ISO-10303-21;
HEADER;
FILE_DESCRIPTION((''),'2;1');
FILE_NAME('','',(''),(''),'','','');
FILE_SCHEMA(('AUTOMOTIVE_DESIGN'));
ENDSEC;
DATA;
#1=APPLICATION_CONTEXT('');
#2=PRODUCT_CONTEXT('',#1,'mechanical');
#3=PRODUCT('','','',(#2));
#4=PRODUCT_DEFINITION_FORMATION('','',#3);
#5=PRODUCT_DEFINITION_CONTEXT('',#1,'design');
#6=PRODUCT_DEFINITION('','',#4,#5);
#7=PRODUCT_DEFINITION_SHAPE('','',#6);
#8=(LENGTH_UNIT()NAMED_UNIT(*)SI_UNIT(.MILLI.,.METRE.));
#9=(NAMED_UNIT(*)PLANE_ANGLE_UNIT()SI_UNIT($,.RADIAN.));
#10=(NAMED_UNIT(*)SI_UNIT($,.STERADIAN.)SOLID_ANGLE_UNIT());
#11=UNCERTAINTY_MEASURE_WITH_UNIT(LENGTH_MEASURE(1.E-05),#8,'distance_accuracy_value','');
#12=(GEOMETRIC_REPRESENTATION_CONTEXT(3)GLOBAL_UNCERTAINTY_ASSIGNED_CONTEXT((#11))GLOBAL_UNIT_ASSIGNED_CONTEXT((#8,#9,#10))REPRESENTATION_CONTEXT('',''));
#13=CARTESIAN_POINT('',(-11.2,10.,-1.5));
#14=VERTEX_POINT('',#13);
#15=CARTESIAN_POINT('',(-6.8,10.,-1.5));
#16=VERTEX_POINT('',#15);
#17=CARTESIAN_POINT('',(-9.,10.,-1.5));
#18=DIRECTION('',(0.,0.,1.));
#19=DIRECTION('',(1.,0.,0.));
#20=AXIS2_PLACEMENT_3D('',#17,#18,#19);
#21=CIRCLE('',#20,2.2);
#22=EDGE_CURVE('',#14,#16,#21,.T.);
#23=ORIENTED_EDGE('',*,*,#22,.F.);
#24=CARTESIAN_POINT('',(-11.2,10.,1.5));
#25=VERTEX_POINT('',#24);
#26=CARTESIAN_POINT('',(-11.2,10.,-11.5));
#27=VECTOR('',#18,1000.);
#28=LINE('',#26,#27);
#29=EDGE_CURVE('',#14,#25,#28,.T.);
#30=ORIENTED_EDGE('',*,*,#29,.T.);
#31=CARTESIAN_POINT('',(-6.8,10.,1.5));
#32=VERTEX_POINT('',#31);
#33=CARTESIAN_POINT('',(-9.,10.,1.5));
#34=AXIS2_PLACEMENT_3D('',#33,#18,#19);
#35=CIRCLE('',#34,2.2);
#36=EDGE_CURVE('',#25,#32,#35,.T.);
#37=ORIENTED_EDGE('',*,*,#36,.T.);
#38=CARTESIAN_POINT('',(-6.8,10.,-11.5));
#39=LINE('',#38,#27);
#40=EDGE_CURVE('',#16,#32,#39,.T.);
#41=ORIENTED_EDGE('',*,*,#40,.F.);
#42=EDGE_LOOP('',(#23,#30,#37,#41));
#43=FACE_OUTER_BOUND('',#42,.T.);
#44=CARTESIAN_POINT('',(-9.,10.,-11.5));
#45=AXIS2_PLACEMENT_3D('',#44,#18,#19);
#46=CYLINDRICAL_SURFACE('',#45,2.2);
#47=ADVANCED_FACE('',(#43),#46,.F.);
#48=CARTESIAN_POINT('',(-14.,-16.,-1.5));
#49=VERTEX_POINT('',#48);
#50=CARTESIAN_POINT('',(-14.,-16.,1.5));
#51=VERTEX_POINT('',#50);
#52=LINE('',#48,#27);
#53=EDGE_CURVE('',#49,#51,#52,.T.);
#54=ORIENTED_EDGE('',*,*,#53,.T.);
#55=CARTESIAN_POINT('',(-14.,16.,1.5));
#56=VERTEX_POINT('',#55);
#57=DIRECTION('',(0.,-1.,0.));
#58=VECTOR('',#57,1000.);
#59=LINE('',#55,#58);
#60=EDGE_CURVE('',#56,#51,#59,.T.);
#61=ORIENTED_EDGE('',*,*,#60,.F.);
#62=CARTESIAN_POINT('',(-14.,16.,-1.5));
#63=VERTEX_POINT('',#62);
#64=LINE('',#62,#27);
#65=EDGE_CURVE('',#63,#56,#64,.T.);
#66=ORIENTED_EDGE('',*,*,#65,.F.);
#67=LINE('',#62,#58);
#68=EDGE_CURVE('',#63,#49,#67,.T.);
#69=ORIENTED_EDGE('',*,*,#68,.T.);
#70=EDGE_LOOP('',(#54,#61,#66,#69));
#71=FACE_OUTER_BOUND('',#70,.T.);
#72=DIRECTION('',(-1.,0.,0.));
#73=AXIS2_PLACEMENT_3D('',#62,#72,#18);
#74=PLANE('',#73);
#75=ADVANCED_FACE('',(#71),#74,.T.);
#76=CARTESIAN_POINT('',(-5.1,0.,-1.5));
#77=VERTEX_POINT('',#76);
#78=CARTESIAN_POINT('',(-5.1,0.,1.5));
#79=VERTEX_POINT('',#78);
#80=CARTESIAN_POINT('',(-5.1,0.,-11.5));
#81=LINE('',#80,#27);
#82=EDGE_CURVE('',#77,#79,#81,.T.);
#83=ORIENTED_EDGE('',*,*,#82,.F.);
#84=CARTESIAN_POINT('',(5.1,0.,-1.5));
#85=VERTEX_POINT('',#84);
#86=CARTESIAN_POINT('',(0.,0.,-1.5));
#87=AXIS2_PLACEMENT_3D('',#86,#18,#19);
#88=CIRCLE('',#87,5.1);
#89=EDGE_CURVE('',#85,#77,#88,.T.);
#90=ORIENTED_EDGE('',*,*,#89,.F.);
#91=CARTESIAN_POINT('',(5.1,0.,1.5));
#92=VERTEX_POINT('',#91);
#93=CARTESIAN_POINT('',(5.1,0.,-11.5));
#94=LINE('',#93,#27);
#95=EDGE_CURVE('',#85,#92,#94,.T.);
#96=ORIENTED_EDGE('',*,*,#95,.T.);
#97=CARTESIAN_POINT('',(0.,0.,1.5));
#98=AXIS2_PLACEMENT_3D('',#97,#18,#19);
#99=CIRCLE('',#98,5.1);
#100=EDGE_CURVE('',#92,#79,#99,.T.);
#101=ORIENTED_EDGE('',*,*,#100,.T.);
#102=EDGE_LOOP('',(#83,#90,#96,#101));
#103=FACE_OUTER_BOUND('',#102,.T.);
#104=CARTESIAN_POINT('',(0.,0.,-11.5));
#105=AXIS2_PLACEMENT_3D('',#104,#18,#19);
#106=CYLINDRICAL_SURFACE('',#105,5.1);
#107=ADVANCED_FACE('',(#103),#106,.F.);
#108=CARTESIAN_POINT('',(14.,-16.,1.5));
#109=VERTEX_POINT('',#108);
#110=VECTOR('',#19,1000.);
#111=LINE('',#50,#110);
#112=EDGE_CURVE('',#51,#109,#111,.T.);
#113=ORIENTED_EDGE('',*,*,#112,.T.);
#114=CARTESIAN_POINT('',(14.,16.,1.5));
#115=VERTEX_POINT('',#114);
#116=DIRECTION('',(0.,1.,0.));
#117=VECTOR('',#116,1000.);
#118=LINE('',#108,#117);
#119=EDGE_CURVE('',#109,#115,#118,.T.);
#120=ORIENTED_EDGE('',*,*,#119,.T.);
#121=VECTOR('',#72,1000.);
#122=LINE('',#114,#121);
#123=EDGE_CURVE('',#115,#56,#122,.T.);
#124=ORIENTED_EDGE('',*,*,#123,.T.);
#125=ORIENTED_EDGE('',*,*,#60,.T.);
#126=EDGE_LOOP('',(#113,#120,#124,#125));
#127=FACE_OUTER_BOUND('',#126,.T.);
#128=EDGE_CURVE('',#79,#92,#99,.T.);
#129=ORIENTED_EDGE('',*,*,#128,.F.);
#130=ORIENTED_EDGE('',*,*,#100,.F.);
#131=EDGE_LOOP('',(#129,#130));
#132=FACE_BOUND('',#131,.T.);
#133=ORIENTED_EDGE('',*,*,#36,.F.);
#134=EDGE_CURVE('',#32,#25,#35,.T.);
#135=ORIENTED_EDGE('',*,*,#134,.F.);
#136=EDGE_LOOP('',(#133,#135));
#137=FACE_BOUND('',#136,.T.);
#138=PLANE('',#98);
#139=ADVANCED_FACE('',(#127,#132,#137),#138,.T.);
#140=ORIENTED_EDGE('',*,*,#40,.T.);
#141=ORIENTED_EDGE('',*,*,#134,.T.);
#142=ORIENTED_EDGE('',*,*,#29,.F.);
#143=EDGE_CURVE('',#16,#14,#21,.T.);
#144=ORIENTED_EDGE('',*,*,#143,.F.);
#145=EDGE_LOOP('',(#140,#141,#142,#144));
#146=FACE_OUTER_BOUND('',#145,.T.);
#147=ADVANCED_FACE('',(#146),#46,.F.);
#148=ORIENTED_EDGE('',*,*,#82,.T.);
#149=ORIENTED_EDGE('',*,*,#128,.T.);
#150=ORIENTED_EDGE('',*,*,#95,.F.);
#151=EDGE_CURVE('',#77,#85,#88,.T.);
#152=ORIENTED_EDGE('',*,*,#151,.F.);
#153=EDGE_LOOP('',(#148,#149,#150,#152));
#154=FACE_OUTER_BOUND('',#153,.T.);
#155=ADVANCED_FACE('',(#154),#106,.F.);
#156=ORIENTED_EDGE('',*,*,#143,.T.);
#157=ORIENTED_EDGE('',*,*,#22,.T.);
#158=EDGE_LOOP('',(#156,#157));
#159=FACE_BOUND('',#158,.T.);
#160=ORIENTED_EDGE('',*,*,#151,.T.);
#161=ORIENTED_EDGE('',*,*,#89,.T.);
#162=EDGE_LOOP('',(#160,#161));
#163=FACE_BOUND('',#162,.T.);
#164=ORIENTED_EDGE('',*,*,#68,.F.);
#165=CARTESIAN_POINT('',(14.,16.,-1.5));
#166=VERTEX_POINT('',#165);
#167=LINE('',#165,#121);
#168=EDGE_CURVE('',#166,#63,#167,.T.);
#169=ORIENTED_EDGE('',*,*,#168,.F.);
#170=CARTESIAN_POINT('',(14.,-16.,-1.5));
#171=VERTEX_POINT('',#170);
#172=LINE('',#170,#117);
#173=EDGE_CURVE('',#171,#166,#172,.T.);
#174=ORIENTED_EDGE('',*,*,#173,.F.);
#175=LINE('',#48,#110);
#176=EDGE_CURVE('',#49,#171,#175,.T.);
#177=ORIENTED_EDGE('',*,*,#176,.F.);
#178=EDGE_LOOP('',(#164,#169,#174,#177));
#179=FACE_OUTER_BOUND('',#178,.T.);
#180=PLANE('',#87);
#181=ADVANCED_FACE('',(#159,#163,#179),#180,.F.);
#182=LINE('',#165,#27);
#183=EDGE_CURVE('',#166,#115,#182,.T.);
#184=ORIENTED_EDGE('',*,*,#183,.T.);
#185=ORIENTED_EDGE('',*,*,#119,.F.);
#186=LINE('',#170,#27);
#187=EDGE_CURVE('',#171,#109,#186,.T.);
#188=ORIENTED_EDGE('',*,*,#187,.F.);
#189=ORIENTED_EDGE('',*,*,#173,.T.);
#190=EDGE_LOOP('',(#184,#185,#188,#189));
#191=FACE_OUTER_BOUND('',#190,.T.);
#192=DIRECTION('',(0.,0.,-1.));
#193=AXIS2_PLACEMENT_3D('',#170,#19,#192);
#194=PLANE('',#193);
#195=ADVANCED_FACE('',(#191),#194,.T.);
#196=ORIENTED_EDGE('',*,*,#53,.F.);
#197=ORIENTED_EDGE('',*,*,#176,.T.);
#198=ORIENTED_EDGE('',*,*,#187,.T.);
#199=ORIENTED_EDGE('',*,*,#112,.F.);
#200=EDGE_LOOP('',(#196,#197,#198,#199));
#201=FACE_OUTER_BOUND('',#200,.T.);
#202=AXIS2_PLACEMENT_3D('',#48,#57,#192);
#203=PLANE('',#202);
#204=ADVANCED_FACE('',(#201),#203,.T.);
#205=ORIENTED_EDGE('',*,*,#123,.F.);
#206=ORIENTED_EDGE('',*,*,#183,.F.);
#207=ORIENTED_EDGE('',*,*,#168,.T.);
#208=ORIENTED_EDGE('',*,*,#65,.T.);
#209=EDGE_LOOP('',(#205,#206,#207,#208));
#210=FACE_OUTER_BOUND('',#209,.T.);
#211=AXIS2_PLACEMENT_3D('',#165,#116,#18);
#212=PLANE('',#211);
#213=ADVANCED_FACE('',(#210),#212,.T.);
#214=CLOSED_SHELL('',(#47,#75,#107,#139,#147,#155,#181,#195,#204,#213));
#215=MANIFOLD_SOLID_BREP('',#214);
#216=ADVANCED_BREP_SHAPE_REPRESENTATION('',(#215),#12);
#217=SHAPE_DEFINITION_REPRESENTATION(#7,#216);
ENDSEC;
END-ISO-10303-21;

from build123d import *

# Parameters (mm, degrees)
SKETCH_1_W          = 28
SKETCH_1_H          = 32
EXTRUDE_1_DEPTH     = 1.5
SKETCH_2_R          = 5.1
SKETCH_2_R_2        = 2.2
CUT_EXTRUDE_1_DEPTH = 11.5


with BuildPart() as part:
    # 草图1 → 凸台-拉伸1 (new, symmetric)
    with BuildSketch(Plane.XY):
        Rectangle(SKETCH_1_W, SKETCH_1_H)
    extrude(amount=EXTRUDE_1_DEPTH, both=True)

    # 草图2 → 切除-拉伸1 (cut, symmetric)
    with BuildSketch(Plane.XY):
        Circle(SKETCH_2_R)
        with Locations((-9, 10)):
            Circle(SKETCH_2_R_2)
    extrude(amount=CUT_EXTRUDE_1_DEPTH, both=True, mode=Mode.SUBTRACT)


solid = part.part
